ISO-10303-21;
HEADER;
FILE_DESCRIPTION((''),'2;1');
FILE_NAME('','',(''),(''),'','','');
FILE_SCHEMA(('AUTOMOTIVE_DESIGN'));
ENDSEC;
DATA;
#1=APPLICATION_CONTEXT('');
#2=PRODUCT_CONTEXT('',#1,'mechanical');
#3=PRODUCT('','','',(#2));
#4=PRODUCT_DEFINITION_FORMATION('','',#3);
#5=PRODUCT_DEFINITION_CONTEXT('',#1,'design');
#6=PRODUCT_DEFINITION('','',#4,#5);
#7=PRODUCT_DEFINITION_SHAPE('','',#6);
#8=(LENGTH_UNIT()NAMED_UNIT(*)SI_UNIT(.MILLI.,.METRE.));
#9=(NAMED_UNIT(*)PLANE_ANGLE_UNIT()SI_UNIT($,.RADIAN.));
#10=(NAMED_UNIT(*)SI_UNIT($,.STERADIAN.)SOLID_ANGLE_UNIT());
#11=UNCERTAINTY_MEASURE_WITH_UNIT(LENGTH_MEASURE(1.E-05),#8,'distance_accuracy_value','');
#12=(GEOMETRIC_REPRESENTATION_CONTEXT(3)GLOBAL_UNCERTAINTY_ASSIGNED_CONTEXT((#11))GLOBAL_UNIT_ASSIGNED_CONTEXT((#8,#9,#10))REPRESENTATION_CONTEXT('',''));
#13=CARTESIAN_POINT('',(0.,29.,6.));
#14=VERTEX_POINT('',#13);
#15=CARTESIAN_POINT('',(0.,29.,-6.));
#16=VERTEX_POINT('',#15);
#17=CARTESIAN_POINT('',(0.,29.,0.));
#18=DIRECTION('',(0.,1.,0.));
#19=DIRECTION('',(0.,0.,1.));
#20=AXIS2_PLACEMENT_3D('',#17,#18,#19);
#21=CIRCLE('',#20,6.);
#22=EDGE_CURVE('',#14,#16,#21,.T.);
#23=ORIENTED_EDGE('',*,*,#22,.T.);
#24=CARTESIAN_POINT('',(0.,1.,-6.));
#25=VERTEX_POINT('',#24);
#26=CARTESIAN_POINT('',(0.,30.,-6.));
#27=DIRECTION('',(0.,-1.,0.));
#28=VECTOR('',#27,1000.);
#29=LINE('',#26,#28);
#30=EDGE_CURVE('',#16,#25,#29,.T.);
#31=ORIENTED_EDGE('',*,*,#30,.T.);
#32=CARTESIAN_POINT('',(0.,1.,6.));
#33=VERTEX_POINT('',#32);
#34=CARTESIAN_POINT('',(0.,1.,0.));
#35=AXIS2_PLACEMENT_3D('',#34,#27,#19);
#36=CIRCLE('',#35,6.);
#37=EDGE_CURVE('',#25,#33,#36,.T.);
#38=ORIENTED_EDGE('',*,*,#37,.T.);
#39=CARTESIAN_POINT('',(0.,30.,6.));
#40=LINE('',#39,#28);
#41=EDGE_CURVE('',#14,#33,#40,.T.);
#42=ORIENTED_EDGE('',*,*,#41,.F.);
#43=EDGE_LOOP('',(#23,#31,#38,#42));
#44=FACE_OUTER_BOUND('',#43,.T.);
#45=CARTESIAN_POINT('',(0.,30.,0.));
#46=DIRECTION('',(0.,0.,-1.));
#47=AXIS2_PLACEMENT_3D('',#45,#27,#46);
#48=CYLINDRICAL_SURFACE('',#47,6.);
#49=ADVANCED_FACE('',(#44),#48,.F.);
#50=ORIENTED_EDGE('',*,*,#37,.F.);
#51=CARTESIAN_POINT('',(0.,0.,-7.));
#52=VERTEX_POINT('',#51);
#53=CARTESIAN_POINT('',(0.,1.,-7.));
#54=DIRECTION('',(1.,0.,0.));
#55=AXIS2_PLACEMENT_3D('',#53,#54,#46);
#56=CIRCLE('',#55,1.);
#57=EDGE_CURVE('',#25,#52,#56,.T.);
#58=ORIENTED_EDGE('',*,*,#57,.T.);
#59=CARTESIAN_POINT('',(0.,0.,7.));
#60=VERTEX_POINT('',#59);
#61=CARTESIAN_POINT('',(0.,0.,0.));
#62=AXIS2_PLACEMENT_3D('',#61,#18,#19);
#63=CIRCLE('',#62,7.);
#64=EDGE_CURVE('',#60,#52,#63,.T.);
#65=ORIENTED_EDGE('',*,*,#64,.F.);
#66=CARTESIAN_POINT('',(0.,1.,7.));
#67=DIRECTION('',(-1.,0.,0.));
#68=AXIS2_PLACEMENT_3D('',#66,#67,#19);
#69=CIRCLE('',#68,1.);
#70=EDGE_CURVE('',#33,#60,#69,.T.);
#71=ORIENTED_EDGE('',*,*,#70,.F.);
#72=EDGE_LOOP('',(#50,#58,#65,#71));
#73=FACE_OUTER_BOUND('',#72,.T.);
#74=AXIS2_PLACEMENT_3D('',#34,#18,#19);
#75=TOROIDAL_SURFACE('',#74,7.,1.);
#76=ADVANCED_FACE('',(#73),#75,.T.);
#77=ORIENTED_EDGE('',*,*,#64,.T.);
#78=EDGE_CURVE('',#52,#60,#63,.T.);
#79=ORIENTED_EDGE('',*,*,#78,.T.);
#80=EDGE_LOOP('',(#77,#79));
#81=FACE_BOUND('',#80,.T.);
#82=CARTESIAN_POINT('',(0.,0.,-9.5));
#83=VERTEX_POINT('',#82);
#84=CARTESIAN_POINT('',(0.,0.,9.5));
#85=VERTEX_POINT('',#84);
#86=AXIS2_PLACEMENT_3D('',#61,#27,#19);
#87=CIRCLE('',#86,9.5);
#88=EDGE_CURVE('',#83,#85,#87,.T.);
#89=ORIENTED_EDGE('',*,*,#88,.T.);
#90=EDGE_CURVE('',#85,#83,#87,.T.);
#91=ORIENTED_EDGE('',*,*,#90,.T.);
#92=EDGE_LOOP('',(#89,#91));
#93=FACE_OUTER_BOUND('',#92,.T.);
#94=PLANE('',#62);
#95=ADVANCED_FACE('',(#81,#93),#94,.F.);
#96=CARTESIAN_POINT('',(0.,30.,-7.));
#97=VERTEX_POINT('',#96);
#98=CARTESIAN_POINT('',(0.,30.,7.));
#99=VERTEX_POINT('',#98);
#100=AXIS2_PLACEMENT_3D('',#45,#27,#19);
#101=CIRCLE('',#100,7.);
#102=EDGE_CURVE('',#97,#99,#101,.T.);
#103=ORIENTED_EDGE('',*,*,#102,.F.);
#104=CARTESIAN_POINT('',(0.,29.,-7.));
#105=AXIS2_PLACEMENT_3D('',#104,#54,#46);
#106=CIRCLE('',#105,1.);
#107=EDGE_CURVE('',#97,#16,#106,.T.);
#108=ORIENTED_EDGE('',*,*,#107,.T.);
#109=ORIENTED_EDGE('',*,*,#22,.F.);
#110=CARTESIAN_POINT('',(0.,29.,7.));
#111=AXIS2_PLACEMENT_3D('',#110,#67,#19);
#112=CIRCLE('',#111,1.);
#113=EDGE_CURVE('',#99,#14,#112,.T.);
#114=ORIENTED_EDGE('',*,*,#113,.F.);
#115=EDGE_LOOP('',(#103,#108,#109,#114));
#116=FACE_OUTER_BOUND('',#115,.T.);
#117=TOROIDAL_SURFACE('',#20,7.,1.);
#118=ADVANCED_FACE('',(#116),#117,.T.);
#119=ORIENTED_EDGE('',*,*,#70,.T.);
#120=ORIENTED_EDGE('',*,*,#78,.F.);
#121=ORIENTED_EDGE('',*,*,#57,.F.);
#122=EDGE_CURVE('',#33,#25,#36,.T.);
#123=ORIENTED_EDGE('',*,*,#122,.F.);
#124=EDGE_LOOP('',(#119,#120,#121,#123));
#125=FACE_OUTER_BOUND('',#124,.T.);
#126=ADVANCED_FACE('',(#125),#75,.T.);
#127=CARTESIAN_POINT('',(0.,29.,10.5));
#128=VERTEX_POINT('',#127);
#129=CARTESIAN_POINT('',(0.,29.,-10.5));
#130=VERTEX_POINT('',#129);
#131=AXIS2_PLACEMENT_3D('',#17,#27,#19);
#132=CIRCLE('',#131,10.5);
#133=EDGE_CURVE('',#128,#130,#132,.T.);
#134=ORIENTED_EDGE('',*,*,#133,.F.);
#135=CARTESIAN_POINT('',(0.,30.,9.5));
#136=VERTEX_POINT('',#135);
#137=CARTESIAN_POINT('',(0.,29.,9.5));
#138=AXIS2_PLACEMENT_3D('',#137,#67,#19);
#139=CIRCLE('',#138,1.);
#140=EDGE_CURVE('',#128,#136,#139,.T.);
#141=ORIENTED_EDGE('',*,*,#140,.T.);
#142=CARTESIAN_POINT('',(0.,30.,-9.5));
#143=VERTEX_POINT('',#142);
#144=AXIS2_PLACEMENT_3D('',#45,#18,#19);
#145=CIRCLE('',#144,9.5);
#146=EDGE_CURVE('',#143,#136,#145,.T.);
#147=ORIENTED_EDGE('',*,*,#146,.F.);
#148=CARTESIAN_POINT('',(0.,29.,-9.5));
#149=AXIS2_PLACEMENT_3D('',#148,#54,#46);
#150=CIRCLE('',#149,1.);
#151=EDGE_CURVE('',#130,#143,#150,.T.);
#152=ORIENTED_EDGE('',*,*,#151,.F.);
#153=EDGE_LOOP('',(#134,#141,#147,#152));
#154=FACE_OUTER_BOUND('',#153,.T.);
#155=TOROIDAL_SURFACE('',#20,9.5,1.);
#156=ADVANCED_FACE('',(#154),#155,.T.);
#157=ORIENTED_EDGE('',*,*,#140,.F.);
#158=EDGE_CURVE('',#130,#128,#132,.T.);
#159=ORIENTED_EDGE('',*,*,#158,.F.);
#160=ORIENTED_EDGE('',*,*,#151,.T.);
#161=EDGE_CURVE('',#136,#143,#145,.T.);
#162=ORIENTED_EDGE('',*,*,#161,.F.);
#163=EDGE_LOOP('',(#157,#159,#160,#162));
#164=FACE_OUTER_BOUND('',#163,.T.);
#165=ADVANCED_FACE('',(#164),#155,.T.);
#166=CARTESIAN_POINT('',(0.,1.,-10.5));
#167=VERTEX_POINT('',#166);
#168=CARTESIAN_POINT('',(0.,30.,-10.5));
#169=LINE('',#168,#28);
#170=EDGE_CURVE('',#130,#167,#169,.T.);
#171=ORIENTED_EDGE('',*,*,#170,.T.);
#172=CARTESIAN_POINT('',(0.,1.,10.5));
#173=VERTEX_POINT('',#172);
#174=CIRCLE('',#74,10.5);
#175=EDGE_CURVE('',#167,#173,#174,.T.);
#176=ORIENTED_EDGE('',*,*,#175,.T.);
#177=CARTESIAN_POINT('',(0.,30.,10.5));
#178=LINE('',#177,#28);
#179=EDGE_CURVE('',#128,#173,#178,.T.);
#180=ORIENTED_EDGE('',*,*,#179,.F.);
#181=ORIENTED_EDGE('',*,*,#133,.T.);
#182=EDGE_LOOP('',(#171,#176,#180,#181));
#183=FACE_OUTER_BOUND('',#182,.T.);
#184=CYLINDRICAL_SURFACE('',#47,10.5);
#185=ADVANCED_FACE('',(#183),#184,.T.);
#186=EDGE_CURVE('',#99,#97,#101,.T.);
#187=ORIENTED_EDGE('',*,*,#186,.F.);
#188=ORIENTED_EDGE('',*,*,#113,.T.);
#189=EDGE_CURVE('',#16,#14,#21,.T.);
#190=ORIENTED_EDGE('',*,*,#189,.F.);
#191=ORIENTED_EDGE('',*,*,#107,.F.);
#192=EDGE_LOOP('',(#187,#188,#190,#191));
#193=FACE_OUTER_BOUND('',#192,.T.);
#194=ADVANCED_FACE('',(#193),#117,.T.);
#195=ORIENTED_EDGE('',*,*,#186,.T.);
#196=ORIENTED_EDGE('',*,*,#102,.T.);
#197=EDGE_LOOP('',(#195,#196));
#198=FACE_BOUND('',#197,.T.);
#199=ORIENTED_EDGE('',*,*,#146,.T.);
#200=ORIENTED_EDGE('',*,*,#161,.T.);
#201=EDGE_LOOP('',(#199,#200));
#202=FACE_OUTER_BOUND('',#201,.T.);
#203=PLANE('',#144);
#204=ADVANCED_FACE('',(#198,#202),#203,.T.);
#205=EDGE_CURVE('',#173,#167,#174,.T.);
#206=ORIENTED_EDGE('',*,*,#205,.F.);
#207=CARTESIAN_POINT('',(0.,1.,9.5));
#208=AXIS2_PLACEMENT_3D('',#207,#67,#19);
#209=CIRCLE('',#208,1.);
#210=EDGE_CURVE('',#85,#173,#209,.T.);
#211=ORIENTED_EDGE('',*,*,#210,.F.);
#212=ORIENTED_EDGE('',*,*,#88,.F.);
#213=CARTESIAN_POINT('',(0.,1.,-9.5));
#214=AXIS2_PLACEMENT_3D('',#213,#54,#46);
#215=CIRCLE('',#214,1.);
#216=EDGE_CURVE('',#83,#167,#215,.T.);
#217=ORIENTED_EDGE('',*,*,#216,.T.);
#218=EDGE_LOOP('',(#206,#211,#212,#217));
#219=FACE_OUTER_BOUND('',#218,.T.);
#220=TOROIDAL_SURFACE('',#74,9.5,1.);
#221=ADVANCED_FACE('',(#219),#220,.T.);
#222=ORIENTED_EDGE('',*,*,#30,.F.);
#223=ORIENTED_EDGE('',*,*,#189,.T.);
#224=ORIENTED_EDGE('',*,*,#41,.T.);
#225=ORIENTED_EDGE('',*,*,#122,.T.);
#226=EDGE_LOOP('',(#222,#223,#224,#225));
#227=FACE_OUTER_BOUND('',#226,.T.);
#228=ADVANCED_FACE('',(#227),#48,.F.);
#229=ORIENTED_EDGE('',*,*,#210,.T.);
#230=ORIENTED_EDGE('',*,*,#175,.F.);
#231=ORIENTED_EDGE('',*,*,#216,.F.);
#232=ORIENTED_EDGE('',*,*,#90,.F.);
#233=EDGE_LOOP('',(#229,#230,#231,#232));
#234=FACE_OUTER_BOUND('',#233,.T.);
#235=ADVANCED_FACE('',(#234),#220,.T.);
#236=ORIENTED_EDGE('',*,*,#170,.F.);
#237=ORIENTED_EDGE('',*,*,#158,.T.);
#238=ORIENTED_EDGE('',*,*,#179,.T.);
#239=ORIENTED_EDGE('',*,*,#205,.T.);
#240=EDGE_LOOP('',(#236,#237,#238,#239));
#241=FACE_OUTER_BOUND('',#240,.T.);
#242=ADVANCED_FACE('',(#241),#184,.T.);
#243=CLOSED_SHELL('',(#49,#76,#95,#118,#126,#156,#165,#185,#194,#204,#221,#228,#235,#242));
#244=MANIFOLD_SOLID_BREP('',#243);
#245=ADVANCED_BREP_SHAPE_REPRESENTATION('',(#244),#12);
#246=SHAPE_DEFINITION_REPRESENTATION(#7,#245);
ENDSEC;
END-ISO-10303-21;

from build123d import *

# Parameters (mm, degrees)
SKETCH1_R           = 10.5
SKETCH1_R_2         = 6
BOSS_EXTRUDE1_DEPTH = 30
FILLET1_R           = 1


with BuildPart() as part:
    # Sketch1 → Boss-Extrude1 (new body)
    with BuildSketch(Plane(origin=(0, 0, 0), x_dir=(1, 0, 0), z_dir=(0, 1, 0))):
        with Locations(Location((0, 0, 0), (0, 0, 270))):
            Circle(SKETCH1_R)
        with Locations(Location((0, 0, 0), (0, 0, 270))):
            Circle(SKETCH1_R_2, mode=Mode.SUBTRACT)
    extrude(amount=BOSS_EXTRUDE1_DEPTH)

    # Fillet1
    fillet1_edges = [part.edges().sort_by_distance(p)[0] for p in [
        (0, 0, -10.5),
        (0, 30, -10.5),
        (0, 0, -6),
        (0, 30, -6),
    ]]
    fillet(fillet1_edges, radius=FILLET1_R)


solid = part.part
